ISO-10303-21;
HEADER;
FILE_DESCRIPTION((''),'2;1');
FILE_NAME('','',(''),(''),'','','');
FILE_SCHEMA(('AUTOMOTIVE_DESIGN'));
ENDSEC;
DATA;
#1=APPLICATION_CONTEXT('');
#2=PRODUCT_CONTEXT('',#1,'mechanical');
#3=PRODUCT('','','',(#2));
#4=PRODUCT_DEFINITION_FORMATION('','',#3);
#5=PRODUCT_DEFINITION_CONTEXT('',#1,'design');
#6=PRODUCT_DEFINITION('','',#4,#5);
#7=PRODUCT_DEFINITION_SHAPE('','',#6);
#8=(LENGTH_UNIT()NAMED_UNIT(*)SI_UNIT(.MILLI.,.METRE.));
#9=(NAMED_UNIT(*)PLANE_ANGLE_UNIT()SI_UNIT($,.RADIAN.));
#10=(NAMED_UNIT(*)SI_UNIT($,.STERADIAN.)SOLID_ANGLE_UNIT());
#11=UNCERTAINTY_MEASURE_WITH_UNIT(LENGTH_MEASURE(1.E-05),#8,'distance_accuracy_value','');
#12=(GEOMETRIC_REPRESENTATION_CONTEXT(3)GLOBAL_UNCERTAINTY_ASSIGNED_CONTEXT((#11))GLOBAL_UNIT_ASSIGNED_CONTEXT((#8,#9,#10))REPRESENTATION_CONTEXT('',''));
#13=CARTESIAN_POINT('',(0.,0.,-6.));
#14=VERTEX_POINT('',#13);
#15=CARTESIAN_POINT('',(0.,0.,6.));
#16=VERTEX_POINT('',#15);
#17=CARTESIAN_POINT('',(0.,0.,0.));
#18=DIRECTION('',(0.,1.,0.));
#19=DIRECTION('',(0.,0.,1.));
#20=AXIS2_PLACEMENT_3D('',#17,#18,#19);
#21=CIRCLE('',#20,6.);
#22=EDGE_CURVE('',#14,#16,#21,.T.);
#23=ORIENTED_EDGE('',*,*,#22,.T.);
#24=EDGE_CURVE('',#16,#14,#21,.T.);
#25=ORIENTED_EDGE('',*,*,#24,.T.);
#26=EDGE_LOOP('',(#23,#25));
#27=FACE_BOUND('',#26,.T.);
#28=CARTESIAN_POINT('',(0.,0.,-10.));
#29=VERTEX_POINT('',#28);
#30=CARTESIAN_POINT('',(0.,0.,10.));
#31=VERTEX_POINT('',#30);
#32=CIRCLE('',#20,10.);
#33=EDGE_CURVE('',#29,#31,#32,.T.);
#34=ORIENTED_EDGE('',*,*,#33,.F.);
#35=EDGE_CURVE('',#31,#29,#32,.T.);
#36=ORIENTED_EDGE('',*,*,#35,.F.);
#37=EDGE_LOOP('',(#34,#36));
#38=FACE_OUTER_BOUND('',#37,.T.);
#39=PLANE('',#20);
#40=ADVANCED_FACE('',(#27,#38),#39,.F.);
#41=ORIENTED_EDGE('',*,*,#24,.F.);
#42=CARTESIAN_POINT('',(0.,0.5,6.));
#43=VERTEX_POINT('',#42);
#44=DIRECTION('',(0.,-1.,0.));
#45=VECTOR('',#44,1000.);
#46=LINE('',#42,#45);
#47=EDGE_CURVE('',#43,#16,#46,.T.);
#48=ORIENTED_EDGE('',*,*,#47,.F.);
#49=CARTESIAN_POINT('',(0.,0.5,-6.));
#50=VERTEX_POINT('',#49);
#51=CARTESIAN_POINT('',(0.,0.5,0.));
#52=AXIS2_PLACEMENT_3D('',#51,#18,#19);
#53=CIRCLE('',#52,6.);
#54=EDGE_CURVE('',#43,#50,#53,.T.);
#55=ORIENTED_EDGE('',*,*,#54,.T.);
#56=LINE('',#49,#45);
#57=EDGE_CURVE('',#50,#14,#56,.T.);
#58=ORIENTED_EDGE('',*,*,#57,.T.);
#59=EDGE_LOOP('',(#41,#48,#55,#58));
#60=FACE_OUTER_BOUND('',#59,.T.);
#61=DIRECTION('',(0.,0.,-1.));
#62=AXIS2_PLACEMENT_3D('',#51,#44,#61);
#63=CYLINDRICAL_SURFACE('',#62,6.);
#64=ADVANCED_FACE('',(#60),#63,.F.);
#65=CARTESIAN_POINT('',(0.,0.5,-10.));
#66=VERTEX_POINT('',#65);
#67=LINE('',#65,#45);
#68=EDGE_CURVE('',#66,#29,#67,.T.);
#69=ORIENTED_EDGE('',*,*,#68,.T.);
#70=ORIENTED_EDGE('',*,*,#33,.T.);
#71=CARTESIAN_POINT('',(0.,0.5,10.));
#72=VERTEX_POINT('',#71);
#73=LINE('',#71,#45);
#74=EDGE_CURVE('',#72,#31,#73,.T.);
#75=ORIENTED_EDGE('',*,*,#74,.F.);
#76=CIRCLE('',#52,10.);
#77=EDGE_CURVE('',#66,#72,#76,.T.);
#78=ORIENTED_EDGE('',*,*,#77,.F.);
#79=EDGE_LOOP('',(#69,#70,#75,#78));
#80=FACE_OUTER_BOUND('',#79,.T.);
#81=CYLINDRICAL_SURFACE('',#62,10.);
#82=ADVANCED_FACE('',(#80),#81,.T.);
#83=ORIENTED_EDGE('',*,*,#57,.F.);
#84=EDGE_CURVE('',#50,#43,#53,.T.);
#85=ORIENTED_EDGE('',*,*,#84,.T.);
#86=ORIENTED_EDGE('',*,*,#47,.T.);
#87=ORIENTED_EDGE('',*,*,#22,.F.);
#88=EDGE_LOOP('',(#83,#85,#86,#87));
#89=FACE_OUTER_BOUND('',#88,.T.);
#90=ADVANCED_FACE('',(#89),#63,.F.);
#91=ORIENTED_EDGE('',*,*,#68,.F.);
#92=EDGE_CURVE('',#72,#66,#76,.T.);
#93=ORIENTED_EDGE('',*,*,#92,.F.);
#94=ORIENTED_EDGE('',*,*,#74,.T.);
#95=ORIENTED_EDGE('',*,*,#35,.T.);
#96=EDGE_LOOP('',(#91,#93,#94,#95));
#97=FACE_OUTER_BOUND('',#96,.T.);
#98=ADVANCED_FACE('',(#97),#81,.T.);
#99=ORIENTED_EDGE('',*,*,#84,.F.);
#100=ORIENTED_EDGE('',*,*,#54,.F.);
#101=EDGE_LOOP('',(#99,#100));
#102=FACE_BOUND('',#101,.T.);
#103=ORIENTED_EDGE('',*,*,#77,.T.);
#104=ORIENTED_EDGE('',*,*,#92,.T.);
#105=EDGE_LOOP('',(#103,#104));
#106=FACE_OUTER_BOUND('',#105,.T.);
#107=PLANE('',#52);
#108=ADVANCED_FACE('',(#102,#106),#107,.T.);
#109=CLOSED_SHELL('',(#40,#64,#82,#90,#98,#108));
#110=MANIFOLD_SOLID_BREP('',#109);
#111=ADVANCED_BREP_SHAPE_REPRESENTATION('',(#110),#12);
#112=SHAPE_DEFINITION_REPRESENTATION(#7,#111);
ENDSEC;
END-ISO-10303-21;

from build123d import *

# Parameters (mm, degrees)
SKETCH_1_R      = 10
SKETCH_1_R_2    = 6
EXTRUDE_1_DEPTH = 0.5


with BuildPart() as part:
    # 草图1 → 凸台-拉伸1 (new body)
    with BuildSketch(Plane(origin=(0, 0, 0), x_dir=(1, 0, 0), z_dir=(0, 1, 0))):
        with Locations(Location((0, 0, 0), (0, 0, 270))):
            Circle(SKETCH_1_R)
        with Locations(Location((0, 0, 0), (0, 0, 270))):
            Circle(SKETCH_1_R_2, mode=Mode.SUBTRACT)
    extrude(amount=EXTRUDE_1_DEPTH)


solid = part.part
